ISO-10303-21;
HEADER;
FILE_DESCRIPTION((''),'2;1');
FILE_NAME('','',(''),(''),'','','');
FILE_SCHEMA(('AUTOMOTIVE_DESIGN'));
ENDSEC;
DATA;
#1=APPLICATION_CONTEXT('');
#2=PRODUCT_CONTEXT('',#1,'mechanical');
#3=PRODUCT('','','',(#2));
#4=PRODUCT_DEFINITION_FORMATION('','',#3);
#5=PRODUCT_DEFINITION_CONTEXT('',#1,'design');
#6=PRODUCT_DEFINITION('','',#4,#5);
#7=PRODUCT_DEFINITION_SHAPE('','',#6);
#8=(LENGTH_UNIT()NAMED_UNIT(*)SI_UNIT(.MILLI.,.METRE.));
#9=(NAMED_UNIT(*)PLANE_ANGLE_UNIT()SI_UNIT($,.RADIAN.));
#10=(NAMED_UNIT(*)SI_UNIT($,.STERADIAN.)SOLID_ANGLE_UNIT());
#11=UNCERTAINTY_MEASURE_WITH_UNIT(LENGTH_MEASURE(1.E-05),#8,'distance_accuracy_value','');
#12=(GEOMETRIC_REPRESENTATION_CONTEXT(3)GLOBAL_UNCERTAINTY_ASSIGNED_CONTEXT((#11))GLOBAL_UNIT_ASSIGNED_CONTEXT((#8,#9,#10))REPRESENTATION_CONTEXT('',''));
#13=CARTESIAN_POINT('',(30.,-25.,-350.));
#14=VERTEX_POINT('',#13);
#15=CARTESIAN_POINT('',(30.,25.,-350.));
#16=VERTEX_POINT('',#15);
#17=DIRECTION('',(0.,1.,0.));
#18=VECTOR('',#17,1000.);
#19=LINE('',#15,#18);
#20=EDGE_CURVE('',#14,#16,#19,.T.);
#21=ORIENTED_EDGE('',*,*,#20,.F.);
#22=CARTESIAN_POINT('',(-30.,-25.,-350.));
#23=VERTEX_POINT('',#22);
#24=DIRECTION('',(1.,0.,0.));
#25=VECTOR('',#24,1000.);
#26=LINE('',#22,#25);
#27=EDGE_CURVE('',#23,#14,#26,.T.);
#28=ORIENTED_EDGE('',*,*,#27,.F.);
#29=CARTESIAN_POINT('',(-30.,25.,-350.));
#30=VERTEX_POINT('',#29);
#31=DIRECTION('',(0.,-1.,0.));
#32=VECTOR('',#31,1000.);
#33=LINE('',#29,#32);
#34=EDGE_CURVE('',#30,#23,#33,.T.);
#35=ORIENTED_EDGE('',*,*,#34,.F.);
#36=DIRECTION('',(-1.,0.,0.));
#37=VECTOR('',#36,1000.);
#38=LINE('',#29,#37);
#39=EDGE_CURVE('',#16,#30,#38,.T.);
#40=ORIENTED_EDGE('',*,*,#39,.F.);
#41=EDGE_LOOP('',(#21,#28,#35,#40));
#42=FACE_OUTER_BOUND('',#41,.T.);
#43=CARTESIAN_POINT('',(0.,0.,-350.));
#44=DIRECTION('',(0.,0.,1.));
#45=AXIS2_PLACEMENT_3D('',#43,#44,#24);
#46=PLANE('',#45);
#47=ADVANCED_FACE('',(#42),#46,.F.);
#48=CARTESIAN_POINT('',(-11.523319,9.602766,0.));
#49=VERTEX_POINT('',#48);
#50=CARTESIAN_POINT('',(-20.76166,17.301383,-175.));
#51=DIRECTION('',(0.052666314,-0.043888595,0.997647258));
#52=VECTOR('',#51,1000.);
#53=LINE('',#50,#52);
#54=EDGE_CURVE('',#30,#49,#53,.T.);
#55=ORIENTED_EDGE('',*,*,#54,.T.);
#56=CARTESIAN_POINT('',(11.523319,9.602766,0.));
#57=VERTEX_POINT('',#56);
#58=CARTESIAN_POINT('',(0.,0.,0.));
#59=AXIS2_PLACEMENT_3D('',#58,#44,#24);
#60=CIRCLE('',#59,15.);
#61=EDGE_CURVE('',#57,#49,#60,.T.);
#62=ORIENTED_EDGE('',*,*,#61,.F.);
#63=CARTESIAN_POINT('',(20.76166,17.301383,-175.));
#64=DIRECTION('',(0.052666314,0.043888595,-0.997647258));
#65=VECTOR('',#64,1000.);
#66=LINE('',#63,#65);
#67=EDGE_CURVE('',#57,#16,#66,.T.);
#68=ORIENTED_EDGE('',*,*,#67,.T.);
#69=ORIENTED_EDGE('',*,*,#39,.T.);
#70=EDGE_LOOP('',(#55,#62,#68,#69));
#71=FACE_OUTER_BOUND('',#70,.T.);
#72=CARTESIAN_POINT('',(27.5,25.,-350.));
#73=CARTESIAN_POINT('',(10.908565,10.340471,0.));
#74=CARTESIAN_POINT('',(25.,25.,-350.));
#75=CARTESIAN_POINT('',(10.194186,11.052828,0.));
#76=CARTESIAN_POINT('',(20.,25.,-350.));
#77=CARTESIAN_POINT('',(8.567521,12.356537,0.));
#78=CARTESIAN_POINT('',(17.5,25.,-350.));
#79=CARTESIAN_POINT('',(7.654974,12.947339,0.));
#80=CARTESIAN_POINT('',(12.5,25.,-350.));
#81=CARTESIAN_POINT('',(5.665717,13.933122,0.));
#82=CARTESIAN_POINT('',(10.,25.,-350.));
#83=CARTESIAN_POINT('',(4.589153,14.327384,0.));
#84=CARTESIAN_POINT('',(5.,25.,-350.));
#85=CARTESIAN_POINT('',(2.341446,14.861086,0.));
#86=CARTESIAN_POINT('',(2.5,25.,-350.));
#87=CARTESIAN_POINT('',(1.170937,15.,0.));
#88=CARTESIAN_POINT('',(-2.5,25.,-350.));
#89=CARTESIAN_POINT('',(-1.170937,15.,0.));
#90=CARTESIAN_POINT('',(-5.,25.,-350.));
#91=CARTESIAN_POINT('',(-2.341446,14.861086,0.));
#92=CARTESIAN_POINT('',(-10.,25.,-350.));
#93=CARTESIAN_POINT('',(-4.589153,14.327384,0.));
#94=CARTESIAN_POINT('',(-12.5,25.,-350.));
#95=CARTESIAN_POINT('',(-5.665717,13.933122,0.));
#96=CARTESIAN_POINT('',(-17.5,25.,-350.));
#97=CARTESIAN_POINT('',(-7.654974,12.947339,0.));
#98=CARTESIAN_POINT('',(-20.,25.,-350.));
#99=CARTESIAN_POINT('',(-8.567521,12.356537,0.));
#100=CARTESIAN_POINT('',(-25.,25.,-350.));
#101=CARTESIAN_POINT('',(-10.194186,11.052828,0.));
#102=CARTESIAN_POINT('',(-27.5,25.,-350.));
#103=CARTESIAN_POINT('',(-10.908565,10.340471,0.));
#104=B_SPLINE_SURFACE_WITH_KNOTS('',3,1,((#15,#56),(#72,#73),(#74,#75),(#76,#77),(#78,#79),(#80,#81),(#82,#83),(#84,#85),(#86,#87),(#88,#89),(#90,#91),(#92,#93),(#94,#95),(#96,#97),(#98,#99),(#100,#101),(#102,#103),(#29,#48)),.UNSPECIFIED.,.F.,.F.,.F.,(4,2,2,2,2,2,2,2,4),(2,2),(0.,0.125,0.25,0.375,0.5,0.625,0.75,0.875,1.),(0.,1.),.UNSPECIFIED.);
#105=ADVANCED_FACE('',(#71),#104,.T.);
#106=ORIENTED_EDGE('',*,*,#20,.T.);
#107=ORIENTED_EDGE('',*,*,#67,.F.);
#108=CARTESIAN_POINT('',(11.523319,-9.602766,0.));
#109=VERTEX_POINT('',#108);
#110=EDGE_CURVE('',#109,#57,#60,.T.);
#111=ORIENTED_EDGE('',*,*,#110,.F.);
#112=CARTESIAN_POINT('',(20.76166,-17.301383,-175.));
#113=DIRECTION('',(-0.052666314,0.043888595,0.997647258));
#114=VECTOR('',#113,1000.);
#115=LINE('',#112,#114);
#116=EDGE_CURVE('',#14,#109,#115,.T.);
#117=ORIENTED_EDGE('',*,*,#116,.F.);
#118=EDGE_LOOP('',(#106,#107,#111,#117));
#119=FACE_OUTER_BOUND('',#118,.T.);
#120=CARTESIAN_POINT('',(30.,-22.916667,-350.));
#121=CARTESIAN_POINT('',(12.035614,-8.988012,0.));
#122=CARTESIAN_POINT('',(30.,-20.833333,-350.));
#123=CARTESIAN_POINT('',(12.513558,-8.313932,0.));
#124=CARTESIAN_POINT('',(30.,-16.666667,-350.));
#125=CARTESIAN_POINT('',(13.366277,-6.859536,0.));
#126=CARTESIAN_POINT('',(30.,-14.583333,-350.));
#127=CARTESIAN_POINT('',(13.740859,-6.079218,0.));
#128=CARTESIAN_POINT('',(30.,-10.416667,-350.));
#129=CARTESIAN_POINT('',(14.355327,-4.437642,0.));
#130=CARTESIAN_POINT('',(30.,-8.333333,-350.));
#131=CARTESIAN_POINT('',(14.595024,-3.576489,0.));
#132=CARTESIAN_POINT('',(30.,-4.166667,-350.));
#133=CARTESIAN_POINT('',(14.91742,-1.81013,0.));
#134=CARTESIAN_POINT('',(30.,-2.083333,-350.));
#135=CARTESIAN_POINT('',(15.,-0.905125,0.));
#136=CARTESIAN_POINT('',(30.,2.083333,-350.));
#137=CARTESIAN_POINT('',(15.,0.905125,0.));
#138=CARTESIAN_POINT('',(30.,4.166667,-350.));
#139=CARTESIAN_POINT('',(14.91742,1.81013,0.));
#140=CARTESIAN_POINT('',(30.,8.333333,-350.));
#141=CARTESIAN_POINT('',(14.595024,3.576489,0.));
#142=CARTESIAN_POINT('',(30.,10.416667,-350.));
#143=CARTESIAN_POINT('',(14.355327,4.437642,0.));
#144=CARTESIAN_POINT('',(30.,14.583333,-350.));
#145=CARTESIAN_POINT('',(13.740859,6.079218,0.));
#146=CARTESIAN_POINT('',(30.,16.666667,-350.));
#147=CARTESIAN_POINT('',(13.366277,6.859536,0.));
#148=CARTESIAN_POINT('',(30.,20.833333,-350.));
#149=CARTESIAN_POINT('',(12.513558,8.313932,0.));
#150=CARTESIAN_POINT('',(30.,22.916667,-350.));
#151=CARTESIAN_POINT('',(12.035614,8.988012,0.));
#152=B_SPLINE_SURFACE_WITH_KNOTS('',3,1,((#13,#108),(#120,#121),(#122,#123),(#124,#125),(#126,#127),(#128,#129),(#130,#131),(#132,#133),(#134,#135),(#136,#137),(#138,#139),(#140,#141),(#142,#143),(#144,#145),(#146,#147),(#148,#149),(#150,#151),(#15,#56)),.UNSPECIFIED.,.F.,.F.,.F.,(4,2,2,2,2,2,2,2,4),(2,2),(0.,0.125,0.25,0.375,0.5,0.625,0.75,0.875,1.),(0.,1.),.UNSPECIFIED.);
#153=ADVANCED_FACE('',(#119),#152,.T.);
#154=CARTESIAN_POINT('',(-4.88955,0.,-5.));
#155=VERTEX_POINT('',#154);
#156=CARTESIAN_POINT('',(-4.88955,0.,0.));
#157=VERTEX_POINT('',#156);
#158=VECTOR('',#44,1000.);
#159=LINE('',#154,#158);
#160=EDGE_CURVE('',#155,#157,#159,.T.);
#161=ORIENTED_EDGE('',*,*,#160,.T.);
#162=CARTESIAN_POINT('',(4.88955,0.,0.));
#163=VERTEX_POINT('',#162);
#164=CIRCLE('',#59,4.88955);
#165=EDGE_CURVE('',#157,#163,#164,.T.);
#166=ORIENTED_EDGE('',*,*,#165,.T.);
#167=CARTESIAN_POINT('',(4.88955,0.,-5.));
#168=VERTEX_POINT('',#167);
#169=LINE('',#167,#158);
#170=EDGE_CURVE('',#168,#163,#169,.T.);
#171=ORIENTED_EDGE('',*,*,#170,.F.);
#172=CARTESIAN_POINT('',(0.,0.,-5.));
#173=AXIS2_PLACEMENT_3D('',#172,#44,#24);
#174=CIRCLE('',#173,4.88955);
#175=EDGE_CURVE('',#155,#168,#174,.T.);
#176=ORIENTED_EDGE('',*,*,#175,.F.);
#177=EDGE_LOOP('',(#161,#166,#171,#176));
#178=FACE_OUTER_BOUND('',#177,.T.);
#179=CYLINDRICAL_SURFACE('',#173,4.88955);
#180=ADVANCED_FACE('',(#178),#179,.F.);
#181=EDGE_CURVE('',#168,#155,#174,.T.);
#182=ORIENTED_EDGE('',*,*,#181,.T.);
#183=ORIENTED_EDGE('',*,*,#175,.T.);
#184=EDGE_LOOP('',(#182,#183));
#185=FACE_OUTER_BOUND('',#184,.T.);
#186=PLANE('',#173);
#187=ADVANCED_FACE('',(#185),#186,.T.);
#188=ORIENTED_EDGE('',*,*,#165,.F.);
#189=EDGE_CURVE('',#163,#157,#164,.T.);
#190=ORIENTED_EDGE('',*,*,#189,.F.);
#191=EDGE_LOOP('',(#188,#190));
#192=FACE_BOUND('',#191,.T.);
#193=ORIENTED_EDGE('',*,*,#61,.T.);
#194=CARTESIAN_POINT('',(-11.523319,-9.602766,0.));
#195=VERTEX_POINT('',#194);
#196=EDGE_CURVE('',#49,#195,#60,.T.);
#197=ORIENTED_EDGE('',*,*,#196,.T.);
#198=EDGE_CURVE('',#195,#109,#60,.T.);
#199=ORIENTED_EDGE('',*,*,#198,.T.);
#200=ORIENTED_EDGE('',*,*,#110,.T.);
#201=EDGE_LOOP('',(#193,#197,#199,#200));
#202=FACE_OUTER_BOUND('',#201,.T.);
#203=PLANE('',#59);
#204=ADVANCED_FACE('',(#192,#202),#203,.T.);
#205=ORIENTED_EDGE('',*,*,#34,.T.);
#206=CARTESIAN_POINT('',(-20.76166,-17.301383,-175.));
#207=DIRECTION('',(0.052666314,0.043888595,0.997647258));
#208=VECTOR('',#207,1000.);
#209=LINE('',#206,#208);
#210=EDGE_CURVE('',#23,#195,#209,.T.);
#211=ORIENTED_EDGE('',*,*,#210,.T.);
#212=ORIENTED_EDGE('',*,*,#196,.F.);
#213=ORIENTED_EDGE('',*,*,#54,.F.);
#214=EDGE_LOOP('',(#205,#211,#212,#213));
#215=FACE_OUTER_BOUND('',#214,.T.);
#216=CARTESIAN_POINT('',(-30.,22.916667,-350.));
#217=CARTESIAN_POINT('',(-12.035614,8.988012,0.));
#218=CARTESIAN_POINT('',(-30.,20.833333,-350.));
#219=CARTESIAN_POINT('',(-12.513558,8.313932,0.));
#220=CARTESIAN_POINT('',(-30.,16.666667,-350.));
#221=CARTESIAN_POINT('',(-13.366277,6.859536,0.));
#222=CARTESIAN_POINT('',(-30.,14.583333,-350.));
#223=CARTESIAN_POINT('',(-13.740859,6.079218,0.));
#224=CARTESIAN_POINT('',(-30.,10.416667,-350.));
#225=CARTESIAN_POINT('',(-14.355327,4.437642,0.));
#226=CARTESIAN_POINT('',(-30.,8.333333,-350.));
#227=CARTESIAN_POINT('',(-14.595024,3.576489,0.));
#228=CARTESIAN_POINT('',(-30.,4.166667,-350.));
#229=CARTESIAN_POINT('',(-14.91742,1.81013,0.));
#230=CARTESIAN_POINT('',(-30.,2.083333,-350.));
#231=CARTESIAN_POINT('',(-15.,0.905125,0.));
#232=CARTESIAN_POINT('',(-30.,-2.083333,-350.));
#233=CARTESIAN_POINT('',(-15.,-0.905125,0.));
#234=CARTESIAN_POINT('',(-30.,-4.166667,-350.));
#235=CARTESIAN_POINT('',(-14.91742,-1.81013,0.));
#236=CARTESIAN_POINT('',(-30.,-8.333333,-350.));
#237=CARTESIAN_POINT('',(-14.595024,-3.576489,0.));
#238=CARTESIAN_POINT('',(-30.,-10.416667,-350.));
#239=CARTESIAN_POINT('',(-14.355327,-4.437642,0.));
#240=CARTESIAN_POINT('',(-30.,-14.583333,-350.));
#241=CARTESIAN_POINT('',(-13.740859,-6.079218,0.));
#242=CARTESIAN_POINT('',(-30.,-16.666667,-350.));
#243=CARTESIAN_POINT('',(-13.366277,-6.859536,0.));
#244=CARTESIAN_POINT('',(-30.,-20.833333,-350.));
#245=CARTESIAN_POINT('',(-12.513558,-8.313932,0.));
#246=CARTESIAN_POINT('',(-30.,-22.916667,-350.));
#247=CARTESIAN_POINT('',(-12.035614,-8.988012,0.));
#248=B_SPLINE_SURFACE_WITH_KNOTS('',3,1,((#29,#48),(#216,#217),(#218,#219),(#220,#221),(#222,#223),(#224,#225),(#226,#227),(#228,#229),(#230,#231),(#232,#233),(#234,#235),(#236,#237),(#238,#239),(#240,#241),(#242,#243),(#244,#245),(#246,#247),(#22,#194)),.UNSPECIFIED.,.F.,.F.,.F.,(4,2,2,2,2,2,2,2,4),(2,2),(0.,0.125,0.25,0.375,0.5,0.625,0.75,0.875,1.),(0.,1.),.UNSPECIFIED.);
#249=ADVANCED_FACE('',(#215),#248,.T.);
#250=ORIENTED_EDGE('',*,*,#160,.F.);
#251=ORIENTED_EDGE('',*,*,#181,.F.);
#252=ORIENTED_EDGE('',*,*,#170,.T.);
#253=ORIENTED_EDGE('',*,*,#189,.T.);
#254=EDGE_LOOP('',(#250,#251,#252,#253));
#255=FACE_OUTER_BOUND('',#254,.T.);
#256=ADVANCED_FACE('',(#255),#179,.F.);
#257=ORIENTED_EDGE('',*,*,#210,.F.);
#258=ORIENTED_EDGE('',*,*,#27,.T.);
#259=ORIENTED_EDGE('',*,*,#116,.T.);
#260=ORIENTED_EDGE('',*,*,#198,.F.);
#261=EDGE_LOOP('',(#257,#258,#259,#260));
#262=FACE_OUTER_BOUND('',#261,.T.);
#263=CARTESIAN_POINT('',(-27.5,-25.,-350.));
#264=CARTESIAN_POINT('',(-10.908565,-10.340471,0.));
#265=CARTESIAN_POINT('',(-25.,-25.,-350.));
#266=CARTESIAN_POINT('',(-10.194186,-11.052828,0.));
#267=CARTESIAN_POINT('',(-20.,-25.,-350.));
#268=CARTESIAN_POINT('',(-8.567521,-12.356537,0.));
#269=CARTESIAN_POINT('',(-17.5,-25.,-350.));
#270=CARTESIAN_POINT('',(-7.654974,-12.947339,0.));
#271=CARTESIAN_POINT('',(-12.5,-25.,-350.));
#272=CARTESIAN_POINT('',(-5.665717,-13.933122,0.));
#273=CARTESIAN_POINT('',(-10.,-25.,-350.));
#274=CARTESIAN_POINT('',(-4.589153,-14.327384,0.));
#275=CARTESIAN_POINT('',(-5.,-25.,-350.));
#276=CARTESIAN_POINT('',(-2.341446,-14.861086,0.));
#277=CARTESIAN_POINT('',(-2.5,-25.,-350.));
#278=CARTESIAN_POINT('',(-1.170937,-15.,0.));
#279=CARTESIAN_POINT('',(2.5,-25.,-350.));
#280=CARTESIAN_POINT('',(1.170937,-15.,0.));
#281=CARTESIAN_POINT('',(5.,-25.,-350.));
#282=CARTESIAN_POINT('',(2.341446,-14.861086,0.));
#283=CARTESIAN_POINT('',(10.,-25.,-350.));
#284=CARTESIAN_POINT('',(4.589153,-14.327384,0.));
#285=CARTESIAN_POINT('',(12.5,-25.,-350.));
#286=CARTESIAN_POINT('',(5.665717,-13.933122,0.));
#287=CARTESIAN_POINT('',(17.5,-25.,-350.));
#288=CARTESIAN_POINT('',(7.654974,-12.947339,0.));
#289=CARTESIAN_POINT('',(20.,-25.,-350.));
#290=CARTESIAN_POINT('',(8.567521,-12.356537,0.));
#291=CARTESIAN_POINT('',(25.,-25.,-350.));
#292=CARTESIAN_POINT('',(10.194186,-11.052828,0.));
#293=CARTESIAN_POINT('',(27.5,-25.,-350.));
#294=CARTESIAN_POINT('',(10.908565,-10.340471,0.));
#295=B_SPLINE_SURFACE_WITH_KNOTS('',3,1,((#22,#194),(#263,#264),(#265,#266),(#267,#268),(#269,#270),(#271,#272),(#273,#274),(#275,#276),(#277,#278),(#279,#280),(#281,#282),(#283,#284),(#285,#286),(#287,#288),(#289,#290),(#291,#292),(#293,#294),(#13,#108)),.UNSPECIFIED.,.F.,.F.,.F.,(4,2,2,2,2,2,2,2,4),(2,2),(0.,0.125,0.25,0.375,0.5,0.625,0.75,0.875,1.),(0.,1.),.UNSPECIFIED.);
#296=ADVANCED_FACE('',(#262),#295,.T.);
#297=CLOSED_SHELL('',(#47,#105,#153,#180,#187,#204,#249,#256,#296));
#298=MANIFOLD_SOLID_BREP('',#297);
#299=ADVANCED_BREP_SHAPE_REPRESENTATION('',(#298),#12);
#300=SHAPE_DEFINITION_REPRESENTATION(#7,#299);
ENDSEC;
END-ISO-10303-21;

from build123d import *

# Parameters (mm, degrees)
SKETCH_3_R          = 4.889549894
CUT_EXTRUDE_1_DEPTH = 5


with BuildPart() as part:
    # 草图2 → 放样1 section 0
    with BuildSketch(Plane.XY.offset(-350)):
        with BuildLine():
            Line((-30, 25), (30, 25))
            Line((30, 25), (30, -25))
            Line((30, -25), (-30, -25))
            Line((-30, -25), (-30, 25))
        make_face()
    # 草图1 for 放样1 → 放样1 section 1
    with BuildSketch(Plane.XY):
        with BuildLine():
            # circular arc as an exact rational Bezier (weights 1, cos(half-angle), 1)
            Bezier((-11.523319194, 9.602765995), (0, 23.430749028), (11.523319194, 9.602765995), weights=[1, 0.6401844, 1])
            Bezier((11.523319194, 9.602765995), (19.52562419, 0), (11.523319194, -9.602765995), weights=[1, 0.76822128, 1])
            Bezier((11.523319194, -9.602765995), (0, -23.430749028), (-11.523319194, -9.602765995), weights=[1, 0.6401844, 1])
            Bezier((-11.523319194, -9.602765995), (-19.52562419, 0), (-11.523319194, 9.602765995), weights=[1, 0.76822128, 1])
        make_face()
    loft()

    # 草图3 → 切除-拉伸1 (cut)
    with BuildSketch(Plane.XY):
        Circle(SKETCH_3_R)
    extrude(amount=-CUT_EXTRUDE_1_DEPTH, mode=Mode.SUBTRACT)


solid = part.part
